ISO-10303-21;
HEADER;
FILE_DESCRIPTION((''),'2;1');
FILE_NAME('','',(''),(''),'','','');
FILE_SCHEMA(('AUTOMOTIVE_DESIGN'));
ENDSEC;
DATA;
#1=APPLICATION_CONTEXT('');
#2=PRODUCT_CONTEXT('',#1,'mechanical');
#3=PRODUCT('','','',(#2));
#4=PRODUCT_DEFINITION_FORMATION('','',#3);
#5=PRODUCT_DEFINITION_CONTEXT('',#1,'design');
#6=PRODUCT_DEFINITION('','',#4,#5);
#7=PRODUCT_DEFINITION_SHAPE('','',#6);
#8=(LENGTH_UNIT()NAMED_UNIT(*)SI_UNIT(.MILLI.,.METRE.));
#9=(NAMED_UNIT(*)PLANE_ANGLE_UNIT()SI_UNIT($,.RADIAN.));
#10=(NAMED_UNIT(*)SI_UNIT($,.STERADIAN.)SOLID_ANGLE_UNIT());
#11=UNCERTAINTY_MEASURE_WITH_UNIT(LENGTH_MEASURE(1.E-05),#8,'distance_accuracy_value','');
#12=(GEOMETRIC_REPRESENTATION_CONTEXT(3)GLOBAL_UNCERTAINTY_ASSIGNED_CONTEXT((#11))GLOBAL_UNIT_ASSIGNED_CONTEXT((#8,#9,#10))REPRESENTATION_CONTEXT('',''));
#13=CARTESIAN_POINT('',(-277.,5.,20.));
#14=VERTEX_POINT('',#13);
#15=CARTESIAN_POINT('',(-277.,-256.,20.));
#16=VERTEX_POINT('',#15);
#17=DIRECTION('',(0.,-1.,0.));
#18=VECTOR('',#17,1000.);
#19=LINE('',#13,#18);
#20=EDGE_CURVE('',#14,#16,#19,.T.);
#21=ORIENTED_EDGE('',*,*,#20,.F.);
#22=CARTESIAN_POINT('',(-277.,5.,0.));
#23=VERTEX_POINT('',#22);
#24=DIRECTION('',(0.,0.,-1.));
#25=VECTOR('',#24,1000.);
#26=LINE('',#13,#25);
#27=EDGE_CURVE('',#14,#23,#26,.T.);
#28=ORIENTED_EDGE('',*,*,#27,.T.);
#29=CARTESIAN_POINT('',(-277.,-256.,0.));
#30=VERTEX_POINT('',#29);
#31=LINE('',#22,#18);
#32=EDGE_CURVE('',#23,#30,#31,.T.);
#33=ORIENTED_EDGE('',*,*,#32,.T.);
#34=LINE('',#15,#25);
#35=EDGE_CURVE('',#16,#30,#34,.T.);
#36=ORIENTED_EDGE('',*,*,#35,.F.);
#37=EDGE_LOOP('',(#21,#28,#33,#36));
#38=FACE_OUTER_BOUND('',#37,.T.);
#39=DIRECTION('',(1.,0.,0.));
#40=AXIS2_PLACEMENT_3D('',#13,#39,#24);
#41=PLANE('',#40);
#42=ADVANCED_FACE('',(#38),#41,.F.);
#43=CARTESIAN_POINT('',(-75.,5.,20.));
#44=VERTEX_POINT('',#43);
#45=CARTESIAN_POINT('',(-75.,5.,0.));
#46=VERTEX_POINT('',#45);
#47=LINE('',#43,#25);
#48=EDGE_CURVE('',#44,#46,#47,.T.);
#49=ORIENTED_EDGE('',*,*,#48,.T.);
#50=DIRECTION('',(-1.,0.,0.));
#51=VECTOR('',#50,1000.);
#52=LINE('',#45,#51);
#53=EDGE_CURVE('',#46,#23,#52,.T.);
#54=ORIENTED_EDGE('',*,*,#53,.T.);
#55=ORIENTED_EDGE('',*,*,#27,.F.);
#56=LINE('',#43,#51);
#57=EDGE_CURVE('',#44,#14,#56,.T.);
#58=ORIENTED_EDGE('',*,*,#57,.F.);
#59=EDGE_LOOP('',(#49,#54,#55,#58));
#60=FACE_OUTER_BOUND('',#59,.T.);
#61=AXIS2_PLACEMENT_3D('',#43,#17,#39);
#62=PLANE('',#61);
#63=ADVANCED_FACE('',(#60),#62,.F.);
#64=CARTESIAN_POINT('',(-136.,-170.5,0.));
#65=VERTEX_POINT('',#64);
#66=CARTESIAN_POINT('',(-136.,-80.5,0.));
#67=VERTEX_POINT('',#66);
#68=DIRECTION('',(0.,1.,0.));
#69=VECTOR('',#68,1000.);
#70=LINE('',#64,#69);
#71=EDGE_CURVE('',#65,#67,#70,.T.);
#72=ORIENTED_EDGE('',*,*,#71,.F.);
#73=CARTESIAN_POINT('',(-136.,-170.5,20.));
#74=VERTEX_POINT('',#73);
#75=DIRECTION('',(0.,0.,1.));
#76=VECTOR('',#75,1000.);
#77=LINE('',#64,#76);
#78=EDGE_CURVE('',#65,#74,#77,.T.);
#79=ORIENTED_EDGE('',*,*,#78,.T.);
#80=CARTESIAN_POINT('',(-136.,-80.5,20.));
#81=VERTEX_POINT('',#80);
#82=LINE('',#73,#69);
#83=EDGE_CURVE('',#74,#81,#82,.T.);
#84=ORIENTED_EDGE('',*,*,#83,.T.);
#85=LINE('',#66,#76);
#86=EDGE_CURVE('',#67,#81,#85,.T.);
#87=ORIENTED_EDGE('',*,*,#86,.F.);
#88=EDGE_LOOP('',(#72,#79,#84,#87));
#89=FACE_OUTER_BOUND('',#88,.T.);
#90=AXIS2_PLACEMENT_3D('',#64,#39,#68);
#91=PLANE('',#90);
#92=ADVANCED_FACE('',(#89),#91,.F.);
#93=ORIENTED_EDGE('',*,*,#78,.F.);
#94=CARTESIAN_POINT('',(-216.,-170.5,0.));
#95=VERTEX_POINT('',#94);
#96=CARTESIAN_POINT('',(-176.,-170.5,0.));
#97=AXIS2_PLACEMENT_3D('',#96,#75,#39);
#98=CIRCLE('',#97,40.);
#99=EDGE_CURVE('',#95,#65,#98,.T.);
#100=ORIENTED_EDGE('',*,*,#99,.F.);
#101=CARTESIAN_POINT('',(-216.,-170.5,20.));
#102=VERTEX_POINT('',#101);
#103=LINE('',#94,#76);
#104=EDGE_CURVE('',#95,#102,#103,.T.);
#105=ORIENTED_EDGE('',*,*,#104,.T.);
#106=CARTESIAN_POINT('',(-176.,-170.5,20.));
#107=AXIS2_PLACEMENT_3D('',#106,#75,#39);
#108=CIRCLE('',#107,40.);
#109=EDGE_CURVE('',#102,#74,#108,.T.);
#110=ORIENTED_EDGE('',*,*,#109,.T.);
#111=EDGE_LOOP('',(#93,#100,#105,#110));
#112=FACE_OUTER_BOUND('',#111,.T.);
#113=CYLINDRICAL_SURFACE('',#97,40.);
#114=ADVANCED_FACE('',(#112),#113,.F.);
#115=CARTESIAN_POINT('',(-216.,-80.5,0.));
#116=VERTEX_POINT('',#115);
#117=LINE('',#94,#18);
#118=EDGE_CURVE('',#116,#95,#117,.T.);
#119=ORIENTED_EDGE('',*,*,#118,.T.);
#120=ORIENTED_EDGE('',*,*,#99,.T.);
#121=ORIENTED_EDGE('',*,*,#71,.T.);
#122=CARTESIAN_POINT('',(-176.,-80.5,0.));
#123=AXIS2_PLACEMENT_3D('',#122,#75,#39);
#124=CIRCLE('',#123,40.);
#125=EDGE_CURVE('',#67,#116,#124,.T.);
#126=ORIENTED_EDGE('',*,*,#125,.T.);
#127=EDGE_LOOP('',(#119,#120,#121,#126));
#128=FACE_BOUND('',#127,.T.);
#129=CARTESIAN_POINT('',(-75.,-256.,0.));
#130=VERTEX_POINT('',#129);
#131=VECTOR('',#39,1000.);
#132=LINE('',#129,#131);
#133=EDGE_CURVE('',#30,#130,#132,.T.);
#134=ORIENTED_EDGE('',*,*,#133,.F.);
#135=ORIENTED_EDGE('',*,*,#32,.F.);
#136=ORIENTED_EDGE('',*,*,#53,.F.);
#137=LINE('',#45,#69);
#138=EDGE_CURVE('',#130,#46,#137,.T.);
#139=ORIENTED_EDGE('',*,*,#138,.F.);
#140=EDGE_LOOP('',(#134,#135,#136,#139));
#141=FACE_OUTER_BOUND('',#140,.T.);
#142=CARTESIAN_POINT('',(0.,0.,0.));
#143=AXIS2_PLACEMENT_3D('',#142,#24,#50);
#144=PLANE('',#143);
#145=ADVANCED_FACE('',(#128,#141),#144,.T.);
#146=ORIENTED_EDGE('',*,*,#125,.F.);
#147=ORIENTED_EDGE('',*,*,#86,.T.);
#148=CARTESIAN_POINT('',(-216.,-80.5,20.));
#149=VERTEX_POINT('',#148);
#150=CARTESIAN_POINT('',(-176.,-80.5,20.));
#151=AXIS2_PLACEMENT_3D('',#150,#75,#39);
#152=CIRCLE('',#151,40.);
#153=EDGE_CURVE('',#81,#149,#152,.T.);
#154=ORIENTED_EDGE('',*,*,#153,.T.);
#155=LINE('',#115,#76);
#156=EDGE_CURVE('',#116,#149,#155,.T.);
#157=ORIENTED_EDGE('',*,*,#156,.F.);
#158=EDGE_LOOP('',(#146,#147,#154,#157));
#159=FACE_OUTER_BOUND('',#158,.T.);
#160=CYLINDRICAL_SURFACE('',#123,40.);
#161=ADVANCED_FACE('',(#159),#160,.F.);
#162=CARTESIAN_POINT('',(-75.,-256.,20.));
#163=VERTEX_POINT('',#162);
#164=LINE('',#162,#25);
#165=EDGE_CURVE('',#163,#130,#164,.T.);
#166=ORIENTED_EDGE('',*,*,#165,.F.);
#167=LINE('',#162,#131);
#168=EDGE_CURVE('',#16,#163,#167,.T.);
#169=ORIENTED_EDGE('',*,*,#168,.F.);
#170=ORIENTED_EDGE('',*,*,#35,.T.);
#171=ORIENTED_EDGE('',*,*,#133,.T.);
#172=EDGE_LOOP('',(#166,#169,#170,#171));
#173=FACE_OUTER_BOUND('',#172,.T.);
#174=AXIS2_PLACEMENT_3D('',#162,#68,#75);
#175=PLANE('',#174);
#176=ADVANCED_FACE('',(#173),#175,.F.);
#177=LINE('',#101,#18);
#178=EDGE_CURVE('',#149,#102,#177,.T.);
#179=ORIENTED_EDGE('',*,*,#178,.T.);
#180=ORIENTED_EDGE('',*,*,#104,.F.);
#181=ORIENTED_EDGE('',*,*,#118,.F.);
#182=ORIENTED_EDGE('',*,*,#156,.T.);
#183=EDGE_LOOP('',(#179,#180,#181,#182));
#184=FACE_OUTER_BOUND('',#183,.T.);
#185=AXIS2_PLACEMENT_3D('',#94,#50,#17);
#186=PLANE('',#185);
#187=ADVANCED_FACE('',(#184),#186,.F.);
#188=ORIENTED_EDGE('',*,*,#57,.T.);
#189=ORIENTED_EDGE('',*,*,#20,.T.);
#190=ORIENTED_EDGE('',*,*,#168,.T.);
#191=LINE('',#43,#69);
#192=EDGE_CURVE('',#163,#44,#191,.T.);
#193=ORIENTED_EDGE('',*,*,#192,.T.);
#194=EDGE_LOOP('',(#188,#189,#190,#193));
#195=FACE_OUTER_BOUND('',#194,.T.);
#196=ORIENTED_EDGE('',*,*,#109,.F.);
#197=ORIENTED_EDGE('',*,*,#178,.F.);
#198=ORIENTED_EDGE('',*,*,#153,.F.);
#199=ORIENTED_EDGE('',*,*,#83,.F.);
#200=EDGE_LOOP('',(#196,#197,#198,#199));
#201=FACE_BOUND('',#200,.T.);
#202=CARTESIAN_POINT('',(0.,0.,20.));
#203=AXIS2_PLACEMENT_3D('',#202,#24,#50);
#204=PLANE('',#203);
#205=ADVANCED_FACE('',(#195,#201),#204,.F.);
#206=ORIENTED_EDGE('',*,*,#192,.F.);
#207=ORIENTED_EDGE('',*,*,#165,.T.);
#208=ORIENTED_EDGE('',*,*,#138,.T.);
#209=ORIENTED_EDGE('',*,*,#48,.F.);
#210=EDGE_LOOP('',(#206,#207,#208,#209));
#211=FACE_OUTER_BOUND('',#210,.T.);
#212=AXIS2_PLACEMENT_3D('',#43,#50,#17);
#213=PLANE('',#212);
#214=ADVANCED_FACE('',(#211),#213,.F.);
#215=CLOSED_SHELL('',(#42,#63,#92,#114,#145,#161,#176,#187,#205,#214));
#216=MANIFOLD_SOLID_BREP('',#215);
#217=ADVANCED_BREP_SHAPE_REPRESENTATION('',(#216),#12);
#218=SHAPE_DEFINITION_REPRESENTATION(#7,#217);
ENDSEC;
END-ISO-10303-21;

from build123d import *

# Parameters (mm, degrees)
SKETCH_1_W          = 202
SKETCH_1_H          = 261
EXTRUDE_1_DEPTH     = 20
CUT_EXTRUDE_1_DEPTH = 378.710206375


with BuildPart() as part:
    # 草图1 → 凸台-拉伸1 (new body)
    with BuildSketch(Plane.XY):
        with Locations((-176, -125.5)):
            Rectangle(SKETCH_1_W, SKETCH_1_H)
    extrude(amount=EXTRUDE_1_DEPTH)

    # 草图2 → 切除-拉伸1 (cut, through all)
    with BuildSketch(Plane.XY.offset(20)):
        with BuildLine():
            Line((-216, -170.5), (-216, -80.5))
            ThreePointArc((-216, -80.5), (-176, -40.5), (-136, -80.5))
            Line((-136, -80.5), (-136, -170.5))
            ThreePointArc((-136, -170.5), (-176, -210.5), (-216, -170.5))
        make_face()
    extrude(amount=-CUT_EXTRUDE_1_DEPTH, mode=Mode.SUBTRACT)


solid = part.part
